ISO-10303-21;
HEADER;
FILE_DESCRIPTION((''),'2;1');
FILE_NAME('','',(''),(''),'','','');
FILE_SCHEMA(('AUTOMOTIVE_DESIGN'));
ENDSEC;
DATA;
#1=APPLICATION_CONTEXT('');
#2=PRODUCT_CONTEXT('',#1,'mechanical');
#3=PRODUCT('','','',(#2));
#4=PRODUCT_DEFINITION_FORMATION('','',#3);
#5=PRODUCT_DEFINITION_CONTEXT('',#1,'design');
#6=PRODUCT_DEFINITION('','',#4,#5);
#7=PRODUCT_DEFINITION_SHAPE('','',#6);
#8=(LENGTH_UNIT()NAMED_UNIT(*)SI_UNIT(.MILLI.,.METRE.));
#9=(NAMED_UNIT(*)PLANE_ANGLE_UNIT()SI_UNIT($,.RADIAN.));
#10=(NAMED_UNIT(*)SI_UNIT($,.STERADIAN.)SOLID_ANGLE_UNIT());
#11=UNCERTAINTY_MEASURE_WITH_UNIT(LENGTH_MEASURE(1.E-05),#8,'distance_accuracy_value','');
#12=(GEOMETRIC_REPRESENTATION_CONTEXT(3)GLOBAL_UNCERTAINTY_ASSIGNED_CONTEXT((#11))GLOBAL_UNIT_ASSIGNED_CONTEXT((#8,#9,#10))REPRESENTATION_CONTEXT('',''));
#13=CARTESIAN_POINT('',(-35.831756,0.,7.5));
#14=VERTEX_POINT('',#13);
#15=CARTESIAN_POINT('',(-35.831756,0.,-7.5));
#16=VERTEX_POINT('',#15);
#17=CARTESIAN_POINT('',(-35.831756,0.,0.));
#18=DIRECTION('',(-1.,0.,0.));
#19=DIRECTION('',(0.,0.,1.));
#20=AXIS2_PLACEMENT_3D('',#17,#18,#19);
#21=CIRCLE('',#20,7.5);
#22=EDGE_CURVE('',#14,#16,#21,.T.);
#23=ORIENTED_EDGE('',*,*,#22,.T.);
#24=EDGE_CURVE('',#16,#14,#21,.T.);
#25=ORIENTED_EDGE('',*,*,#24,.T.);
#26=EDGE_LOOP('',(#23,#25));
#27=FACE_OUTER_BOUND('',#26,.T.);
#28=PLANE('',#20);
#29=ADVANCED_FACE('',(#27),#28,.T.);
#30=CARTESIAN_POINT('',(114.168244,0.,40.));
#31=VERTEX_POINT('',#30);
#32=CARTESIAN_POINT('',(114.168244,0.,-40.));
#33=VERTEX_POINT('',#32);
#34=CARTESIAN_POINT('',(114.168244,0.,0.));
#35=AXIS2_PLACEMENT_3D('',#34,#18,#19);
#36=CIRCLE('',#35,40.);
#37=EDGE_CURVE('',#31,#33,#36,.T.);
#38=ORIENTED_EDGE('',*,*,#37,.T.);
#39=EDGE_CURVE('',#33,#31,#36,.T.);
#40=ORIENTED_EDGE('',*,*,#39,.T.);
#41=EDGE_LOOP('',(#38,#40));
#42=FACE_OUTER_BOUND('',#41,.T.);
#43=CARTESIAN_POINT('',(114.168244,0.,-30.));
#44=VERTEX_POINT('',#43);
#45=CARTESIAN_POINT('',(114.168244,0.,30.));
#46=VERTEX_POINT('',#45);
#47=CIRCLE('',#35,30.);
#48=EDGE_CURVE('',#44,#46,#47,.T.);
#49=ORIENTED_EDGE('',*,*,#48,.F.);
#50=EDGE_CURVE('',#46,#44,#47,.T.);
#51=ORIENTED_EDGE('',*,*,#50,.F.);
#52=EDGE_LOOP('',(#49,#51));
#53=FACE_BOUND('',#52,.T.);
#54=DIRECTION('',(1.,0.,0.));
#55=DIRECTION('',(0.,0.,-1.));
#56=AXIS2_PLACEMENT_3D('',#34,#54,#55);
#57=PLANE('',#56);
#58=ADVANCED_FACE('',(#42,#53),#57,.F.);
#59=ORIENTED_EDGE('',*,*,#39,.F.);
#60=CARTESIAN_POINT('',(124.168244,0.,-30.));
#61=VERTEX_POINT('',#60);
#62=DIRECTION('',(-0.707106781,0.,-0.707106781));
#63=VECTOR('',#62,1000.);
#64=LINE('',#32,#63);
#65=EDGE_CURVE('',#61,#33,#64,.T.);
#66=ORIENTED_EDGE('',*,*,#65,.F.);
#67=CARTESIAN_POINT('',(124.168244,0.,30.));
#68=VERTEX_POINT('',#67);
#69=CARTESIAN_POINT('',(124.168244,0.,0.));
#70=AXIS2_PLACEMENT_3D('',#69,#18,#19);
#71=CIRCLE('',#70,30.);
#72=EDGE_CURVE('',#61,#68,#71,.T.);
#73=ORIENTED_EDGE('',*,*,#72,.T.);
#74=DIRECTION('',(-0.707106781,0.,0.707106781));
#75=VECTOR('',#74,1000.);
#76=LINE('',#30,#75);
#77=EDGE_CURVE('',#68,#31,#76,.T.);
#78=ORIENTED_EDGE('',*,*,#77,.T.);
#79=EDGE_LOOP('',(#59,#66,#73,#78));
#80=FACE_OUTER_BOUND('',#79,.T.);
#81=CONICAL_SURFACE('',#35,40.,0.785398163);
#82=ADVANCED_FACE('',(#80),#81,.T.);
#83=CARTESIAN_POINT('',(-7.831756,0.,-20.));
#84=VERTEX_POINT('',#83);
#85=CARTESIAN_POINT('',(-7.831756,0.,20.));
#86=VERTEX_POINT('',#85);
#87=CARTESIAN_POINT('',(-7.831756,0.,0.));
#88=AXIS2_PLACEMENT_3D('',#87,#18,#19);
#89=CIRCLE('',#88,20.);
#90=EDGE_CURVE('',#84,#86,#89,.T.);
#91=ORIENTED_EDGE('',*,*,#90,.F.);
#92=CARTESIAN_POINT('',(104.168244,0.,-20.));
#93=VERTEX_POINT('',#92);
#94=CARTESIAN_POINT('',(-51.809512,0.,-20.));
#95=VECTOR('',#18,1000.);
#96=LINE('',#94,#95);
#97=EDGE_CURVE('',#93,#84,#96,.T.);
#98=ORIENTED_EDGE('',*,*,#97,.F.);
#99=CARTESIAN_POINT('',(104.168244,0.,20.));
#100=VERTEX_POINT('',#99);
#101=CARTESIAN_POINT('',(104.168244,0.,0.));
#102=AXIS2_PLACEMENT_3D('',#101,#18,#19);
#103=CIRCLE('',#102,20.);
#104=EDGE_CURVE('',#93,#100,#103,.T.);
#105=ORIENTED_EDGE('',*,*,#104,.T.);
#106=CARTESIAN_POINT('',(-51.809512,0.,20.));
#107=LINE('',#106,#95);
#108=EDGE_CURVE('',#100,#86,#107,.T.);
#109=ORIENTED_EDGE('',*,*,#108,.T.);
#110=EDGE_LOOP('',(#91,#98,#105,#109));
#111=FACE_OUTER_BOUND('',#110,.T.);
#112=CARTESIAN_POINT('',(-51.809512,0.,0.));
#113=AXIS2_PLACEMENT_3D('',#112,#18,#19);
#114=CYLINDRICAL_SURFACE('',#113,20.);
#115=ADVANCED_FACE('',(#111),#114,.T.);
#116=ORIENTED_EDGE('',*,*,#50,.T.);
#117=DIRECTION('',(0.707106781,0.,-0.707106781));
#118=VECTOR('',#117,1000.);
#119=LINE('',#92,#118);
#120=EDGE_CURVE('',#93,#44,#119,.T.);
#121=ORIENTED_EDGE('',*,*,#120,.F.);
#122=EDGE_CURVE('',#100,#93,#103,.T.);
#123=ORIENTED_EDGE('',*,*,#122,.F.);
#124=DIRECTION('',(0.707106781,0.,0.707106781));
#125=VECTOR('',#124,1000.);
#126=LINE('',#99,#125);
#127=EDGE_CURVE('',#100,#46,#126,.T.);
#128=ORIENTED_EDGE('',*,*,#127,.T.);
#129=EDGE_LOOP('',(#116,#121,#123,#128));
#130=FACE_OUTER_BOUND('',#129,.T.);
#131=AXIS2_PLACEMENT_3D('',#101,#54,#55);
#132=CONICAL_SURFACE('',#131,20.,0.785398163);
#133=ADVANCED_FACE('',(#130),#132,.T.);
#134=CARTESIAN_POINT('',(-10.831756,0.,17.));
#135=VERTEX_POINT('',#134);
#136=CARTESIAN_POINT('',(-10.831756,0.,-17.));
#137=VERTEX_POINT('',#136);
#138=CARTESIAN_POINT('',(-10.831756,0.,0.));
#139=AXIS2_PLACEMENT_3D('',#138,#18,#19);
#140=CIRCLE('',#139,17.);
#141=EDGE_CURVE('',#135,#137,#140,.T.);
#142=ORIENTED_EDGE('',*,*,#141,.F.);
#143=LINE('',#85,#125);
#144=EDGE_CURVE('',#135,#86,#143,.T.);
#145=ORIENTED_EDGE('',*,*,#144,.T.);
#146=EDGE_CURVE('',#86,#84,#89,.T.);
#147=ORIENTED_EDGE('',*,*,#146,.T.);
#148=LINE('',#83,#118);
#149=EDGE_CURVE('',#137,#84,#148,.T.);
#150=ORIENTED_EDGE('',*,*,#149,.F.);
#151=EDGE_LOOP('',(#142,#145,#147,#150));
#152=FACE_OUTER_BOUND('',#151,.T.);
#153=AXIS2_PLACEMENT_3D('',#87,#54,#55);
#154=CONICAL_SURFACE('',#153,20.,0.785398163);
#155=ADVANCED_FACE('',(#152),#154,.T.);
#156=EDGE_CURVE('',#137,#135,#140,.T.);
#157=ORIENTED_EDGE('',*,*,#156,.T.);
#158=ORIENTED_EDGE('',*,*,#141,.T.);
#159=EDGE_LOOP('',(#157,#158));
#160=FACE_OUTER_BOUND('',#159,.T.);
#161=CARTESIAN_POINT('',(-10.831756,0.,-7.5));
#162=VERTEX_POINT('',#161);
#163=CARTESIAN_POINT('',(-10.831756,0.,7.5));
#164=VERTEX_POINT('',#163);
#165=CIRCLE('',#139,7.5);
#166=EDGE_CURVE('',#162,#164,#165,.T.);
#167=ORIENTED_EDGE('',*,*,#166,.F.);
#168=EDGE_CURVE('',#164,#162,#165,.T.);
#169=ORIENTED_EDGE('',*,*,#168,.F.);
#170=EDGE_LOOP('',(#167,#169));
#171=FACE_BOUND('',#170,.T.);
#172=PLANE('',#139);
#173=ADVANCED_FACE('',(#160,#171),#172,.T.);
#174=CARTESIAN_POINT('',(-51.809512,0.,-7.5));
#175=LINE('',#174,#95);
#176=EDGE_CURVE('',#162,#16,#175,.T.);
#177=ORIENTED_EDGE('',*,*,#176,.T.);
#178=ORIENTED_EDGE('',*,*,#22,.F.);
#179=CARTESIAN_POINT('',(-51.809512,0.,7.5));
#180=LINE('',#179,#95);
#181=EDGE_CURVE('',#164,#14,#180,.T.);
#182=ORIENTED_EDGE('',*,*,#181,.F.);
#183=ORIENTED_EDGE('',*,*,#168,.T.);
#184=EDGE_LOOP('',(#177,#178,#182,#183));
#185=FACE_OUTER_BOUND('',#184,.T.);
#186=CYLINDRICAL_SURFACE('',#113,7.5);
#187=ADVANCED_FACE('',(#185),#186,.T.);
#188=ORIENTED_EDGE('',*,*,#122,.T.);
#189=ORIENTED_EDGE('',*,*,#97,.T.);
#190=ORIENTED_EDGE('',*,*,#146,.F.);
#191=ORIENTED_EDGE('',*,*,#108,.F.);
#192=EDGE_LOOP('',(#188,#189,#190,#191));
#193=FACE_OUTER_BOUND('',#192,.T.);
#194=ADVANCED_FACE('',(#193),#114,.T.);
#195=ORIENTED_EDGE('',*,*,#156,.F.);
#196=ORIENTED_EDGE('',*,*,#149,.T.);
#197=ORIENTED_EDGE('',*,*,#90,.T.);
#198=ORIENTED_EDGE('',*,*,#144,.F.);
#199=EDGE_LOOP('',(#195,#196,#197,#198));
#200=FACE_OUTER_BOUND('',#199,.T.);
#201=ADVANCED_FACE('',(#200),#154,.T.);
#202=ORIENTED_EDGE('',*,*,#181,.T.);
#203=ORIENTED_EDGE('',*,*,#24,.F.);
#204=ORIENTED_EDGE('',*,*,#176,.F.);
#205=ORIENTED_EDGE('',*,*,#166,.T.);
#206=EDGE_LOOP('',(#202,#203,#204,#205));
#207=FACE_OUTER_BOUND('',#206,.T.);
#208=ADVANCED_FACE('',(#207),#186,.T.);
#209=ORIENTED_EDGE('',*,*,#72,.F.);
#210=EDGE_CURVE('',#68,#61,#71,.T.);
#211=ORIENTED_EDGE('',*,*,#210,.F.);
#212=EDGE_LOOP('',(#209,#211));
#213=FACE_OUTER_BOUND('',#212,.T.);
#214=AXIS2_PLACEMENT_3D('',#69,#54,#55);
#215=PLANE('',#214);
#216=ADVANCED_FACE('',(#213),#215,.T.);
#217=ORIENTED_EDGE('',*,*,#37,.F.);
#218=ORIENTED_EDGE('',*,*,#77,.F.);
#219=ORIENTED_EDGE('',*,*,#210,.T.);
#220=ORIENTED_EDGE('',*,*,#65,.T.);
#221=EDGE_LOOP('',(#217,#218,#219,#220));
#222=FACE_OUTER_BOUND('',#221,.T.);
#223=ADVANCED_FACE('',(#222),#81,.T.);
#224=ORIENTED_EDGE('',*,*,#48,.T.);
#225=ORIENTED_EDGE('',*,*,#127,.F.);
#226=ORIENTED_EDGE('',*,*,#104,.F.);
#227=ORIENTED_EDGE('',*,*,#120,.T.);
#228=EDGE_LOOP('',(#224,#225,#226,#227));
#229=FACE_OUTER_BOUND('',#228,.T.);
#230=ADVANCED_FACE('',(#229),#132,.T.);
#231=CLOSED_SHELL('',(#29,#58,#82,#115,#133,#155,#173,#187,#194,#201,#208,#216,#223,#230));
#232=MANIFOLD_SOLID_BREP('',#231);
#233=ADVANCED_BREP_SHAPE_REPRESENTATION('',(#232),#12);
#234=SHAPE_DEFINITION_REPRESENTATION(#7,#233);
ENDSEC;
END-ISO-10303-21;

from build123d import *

# Parameters (mm, degrees)
PLUNGER_PROFILE_SKETCH_W   = 25
PLUNGER_PROFILE_SKETCH_H   = 7.5
PLUNGER_PROFILE_SKETCH_W_2 = 112
PLUNGER_PROFILE_SKETCH_H_2 = 20


with BuildPart() as part:
    # Plunger Profile Sketch → Plunger Body Revolve (revolve)
    with BuildSketch(Plane.XY, mode=Mode.PRIVATE) as plunger_body_revolve_sk:
        with Locations((-23.33175597, 3.75)):
            Rectangle(PLUNGER_PROFILE_SKETCH_W, PLUNGER_PROFILE_SKETCH_H)
        Polygon((-10.83175597, 7.5), (-10.83175597, 0), (-7.83175597, 0), (-7.83175597, 20), (-10.83175597, 17), align=None)
        with Locations((48.16824403, 10)):
            Rectangle(PLUNGER_PROFILE_SKETCH_W_2, PLUNGER_PROFILE_SKETCH_H_2)
        Polygon((104.16824403, 20), (104.16824403, 0), (114.16824403, 0), (114.16824403, 30), align=None)
        Polygon((114.16824403, 30), (114.16824403, 0), (124.16824403, 0), (124.16824403, 30), (114.16824403, 40), align=None)
    revolve(plunger_body_revolve_sk.sketch.rotate(Axis((-51.8095123, 0, 0), (1, 0, 0)), 90), axis=Axis((-51.8095123, 0, 0), (1, 0, 0)))


solid = part.part
